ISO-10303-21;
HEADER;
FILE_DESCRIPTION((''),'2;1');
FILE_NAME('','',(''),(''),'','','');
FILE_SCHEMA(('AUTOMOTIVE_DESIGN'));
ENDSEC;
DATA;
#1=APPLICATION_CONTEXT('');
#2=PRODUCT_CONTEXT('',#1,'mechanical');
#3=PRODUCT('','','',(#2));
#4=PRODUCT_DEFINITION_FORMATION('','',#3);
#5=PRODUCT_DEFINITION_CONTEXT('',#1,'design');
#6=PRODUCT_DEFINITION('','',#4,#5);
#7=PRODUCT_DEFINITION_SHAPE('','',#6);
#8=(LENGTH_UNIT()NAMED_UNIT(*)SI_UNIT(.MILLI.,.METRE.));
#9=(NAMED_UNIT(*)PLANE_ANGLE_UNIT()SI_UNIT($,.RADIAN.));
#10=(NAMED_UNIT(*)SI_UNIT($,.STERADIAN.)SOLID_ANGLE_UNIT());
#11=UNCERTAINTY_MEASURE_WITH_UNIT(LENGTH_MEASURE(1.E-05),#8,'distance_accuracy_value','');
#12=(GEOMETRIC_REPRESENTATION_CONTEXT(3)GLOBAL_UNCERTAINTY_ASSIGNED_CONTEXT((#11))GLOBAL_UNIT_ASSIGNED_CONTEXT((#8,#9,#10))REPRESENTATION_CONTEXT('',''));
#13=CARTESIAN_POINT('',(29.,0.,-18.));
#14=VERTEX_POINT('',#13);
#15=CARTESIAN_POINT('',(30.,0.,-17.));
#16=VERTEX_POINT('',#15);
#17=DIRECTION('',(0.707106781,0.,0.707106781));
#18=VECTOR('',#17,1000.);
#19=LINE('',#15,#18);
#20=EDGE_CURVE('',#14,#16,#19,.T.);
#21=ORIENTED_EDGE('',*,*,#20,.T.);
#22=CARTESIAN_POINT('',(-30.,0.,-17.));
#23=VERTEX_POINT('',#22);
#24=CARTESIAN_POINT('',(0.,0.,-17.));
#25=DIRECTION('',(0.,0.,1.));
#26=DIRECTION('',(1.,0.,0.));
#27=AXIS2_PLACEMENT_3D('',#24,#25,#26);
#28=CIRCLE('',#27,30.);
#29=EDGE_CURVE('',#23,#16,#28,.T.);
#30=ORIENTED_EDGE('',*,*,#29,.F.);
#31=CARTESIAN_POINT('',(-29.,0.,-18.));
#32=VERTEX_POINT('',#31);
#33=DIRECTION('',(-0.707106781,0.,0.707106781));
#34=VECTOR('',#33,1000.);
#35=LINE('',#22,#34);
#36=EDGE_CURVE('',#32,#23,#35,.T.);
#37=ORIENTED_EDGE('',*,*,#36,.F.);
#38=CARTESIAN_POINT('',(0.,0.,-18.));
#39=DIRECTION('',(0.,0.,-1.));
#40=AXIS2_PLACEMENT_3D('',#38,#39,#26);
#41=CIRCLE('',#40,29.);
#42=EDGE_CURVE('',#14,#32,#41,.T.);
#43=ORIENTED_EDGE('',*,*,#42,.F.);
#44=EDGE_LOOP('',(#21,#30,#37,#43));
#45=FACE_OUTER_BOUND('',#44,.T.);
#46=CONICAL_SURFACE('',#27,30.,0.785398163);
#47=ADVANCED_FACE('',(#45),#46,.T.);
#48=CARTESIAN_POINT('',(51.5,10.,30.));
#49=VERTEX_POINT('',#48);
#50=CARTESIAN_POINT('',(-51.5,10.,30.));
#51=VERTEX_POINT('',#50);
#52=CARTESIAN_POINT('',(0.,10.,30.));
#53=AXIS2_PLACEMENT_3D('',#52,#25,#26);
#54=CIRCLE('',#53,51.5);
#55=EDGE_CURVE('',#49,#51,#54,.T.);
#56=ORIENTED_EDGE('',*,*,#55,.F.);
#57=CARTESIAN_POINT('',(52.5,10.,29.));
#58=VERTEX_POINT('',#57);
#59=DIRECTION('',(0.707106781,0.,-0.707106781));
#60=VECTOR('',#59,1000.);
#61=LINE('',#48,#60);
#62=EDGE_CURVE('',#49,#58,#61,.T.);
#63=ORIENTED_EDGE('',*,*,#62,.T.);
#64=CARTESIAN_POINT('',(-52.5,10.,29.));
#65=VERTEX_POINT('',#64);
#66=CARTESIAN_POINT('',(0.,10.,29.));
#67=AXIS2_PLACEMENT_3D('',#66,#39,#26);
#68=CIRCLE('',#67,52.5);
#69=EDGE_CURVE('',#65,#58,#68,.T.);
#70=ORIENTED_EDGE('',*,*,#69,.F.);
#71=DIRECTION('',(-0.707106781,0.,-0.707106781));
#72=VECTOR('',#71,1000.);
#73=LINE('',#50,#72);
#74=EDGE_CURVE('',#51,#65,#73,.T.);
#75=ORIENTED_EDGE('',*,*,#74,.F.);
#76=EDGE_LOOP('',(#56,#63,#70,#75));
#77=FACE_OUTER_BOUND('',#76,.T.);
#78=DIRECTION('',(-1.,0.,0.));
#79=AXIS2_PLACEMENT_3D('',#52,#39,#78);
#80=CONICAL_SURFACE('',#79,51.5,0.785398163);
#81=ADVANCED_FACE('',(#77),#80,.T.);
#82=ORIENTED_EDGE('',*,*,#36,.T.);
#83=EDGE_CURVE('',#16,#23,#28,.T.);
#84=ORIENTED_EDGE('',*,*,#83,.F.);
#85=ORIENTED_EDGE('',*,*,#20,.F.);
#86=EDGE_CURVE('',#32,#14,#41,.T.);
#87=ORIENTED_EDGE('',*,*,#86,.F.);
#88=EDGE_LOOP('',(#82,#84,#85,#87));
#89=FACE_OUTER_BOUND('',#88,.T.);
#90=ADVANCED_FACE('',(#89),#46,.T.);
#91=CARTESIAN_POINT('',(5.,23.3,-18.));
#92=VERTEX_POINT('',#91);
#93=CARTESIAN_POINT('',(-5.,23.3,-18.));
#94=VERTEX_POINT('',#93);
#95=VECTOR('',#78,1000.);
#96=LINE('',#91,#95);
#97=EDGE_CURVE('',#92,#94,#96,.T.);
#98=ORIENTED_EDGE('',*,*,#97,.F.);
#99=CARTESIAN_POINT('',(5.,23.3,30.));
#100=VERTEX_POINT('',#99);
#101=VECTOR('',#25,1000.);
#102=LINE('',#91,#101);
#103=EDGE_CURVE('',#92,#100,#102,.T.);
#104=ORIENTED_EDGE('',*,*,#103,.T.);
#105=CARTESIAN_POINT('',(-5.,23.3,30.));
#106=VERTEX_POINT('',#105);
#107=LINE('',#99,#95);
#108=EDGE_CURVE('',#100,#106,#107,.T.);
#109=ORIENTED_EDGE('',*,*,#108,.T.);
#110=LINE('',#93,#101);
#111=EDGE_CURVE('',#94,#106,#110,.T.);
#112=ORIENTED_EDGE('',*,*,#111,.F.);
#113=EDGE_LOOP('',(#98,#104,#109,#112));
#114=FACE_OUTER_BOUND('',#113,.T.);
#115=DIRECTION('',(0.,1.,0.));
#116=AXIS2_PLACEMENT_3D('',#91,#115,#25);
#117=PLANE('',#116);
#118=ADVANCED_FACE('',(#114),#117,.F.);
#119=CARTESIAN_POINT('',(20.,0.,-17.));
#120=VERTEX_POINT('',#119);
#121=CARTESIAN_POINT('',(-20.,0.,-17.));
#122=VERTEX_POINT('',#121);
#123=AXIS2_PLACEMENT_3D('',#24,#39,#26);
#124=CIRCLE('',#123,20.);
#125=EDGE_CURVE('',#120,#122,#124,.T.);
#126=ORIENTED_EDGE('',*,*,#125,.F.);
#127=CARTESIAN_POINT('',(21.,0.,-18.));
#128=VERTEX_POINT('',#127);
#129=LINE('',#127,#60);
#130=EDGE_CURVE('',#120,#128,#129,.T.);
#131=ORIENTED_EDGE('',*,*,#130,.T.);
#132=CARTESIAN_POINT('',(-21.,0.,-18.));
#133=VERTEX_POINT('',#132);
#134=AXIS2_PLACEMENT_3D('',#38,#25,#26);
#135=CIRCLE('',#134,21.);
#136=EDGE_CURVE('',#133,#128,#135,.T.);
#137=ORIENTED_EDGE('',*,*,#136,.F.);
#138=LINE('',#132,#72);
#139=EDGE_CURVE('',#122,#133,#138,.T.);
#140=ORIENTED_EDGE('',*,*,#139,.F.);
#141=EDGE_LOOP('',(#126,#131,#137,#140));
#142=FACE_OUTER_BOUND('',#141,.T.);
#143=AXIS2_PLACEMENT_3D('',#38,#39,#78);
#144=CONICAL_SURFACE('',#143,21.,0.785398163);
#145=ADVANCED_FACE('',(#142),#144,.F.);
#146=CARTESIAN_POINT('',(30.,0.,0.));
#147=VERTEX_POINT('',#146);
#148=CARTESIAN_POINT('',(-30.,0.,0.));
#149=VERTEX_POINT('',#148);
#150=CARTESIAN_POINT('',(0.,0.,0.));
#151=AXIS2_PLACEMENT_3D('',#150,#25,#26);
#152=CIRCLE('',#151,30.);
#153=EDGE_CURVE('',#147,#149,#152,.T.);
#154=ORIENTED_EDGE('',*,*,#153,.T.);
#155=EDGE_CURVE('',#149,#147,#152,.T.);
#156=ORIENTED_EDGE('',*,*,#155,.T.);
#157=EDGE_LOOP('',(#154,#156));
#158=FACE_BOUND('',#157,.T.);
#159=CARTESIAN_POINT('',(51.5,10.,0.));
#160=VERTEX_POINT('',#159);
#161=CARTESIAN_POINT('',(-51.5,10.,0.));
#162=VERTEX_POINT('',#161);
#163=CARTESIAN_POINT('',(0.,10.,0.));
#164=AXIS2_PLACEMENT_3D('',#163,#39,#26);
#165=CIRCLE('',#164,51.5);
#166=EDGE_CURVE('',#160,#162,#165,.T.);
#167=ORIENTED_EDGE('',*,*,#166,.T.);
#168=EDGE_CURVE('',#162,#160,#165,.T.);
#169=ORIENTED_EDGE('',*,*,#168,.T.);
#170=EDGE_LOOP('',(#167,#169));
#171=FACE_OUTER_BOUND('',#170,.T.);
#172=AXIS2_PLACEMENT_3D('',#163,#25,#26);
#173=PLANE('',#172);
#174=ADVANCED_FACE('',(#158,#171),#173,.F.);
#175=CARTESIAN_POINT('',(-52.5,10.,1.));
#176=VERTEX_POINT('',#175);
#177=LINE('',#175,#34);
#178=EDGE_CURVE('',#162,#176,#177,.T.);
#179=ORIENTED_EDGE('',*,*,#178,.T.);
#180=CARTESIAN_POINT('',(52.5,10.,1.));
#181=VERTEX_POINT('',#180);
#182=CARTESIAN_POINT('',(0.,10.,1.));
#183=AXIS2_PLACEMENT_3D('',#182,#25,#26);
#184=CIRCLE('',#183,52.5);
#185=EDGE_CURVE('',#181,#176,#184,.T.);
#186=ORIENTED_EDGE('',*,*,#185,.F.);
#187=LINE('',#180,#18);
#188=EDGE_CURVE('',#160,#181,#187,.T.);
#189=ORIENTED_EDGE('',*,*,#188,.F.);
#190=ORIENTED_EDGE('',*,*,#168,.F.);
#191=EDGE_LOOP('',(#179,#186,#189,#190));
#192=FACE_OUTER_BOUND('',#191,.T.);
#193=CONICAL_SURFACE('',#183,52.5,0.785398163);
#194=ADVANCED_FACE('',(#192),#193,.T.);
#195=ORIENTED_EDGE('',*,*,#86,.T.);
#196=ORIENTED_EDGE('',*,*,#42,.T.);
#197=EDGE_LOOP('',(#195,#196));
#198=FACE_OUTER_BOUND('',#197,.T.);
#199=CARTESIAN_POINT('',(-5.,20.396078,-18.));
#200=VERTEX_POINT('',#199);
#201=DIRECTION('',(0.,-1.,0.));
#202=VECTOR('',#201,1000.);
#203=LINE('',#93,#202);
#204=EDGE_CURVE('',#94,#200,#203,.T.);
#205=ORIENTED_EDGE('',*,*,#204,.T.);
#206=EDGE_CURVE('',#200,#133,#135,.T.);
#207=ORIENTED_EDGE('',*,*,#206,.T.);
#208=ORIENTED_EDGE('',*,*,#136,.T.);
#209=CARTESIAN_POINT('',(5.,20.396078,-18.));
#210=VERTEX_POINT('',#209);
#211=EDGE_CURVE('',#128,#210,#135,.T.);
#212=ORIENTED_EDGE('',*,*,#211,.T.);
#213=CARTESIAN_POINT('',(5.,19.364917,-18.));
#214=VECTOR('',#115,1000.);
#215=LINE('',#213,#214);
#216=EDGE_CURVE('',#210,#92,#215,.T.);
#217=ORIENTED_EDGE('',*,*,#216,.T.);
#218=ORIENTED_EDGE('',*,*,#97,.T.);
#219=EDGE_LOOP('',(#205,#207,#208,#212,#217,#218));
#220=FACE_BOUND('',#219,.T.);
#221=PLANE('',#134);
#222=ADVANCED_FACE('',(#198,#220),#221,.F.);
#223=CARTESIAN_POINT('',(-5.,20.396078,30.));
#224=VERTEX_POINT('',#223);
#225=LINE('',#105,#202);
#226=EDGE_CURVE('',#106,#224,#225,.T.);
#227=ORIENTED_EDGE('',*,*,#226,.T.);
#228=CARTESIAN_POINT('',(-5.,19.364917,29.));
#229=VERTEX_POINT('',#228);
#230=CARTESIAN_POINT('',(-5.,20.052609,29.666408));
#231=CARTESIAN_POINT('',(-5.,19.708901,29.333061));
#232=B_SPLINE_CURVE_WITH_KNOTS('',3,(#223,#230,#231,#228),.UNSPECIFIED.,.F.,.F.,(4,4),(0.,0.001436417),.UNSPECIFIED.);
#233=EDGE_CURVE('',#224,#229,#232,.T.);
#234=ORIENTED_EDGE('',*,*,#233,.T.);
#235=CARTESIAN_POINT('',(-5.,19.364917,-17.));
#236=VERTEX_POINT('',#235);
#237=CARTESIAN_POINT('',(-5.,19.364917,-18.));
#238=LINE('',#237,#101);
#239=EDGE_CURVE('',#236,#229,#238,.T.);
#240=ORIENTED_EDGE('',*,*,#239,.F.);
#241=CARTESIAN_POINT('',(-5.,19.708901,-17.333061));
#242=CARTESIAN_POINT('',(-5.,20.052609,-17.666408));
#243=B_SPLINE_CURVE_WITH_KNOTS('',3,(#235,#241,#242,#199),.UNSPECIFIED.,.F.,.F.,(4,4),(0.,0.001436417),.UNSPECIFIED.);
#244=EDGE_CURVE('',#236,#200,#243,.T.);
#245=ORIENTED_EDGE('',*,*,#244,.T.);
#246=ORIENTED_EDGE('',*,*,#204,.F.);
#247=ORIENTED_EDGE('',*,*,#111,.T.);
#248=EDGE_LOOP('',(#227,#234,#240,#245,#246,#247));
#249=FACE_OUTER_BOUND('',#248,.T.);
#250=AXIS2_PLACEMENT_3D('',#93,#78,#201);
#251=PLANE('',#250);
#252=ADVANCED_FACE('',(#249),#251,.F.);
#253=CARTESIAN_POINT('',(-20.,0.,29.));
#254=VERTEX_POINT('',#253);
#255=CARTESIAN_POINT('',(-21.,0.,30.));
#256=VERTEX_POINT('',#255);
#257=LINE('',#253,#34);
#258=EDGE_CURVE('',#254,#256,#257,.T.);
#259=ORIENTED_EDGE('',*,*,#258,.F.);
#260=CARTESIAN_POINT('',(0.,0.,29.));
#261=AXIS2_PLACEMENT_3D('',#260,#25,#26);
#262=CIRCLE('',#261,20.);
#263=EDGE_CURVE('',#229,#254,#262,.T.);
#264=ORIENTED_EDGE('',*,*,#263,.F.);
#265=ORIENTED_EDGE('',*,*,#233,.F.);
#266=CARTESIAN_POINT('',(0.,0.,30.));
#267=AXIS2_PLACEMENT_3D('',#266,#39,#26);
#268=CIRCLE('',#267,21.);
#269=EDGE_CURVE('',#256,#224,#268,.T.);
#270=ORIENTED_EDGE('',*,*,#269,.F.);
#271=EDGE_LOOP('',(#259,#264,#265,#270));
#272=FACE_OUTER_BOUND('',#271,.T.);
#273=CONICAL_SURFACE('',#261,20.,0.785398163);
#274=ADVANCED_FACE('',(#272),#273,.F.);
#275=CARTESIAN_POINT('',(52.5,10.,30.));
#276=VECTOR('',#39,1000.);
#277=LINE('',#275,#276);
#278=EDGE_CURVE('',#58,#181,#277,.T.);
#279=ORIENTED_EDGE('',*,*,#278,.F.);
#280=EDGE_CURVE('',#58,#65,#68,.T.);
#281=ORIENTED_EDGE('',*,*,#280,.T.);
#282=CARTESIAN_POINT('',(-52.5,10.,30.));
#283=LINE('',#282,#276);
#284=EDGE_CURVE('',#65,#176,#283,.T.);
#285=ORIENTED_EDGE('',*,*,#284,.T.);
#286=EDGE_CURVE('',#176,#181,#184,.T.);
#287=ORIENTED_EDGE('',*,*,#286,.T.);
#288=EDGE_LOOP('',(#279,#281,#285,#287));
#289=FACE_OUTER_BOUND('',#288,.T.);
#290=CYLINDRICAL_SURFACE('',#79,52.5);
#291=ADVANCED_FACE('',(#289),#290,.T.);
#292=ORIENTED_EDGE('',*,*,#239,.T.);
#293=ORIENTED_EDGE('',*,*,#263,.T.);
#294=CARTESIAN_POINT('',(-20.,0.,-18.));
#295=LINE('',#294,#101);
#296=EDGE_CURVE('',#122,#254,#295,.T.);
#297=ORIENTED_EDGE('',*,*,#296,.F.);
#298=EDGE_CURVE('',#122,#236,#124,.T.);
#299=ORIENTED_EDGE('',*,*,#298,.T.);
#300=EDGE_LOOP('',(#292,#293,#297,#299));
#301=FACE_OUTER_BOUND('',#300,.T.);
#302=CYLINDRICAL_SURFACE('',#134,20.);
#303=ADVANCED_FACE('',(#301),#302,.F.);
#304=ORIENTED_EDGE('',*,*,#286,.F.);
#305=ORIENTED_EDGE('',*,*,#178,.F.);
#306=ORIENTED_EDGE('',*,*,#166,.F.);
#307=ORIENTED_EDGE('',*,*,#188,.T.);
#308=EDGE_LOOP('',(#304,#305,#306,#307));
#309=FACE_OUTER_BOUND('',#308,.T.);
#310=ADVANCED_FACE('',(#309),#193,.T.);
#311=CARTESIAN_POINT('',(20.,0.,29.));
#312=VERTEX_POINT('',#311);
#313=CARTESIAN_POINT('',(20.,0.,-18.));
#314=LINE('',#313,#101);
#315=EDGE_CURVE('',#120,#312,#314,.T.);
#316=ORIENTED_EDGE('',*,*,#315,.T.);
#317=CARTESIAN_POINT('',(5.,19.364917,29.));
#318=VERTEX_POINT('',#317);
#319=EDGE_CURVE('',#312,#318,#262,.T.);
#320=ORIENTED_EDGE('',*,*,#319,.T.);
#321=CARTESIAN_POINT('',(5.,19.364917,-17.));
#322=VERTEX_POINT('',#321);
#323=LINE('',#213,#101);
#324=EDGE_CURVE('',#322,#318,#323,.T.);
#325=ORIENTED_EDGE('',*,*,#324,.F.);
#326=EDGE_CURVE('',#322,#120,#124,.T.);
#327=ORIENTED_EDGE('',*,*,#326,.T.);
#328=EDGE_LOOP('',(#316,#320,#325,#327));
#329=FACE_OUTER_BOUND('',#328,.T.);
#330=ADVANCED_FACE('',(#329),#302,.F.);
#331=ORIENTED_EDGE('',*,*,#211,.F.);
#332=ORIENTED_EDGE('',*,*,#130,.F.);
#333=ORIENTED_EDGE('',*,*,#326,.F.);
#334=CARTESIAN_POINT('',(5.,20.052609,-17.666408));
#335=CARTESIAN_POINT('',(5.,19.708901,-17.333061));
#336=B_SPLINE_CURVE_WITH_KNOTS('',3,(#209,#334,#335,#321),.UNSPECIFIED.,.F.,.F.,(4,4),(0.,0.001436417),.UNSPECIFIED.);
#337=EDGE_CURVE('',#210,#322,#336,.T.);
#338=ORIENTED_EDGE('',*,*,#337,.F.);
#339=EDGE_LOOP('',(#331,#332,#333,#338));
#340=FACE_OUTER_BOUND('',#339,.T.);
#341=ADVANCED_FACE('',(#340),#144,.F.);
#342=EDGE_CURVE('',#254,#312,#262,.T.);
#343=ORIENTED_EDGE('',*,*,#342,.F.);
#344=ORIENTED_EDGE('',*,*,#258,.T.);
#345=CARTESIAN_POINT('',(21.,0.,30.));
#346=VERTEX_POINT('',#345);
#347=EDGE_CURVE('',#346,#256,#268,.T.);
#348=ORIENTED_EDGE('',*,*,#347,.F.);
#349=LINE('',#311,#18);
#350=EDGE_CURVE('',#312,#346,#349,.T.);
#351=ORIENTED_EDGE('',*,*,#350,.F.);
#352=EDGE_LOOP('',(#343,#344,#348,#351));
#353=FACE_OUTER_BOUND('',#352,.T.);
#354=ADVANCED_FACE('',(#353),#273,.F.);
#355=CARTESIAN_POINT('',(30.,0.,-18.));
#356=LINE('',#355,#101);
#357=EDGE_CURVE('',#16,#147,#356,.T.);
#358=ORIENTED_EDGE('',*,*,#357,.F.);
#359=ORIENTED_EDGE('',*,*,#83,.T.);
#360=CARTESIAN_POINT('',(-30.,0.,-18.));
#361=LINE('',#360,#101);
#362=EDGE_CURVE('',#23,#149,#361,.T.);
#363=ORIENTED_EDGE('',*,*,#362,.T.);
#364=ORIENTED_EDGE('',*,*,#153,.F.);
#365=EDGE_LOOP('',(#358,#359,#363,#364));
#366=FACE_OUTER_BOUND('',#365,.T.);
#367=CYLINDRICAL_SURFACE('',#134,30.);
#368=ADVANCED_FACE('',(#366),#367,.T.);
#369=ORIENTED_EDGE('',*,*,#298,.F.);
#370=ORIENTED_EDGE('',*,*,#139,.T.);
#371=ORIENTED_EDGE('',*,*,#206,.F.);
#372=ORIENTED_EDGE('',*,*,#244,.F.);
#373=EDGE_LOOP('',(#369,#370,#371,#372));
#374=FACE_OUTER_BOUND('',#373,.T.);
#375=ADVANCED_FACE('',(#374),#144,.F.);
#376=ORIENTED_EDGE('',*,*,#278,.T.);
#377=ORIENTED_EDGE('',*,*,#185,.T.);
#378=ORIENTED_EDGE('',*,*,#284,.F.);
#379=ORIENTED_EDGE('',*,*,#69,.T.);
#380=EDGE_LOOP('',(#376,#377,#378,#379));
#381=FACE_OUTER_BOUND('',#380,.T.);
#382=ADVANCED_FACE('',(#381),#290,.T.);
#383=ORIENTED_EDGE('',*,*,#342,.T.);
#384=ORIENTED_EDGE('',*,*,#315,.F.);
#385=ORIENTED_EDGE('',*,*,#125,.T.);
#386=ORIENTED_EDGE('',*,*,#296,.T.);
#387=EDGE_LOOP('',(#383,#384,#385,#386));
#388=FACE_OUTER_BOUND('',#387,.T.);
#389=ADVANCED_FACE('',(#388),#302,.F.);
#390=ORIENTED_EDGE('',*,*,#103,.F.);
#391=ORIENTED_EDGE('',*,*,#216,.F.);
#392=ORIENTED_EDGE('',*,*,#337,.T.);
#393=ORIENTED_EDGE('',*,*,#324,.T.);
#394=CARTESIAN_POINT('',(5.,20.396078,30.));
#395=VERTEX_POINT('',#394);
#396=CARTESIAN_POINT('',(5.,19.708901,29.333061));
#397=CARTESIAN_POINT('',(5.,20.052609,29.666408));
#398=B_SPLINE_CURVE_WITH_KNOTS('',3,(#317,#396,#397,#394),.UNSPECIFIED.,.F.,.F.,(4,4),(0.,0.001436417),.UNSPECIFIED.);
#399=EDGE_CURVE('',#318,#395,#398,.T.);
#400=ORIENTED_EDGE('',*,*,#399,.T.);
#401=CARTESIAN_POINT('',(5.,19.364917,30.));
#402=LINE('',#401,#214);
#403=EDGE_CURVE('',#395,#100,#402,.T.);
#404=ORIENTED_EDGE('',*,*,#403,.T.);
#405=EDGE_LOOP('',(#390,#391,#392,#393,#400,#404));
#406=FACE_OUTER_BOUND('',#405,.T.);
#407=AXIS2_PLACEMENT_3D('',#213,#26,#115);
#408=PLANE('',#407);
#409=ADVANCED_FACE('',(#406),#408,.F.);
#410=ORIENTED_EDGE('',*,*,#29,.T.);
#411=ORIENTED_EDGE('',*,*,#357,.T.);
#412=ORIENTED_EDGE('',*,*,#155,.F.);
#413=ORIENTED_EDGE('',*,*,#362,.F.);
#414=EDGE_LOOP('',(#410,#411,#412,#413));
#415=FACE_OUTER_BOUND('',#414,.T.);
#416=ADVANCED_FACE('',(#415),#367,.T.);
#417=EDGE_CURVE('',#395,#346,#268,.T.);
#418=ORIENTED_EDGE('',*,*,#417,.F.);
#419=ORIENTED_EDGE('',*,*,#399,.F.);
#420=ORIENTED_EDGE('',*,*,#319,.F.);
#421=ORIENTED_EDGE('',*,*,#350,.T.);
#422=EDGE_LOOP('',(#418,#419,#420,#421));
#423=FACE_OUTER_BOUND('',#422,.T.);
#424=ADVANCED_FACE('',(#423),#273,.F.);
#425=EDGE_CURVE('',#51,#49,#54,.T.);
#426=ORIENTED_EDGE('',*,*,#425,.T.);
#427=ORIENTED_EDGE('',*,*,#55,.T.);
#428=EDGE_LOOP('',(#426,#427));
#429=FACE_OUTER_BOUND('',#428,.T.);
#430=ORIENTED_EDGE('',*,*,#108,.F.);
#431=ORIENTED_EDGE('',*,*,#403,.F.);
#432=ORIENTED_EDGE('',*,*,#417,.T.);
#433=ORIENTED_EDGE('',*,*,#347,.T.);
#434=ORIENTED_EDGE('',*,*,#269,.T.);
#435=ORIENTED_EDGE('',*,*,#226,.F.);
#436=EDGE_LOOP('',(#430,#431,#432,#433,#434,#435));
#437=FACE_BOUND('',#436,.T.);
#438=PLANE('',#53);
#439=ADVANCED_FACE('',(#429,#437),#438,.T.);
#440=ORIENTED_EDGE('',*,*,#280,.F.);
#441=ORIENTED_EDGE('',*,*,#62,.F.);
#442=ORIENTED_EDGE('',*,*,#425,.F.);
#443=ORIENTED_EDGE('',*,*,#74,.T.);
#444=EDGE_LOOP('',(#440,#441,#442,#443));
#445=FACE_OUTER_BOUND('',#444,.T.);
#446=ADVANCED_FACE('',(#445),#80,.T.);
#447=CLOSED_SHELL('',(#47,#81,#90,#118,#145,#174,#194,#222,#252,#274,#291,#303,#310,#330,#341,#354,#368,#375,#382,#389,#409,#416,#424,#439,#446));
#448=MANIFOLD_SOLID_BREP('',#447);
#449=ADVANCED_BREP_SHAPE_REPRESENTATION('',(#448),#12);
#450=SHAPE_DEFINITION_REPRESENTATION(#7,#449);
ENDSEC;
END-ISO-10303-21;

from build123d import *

# Parameters (mm, degrees)
SKETCH_1_4_R       = 52.5
EXTRUDE1_DEPTH     = 30
SKETCH_1_3_R       = 30
EXTRUDE2_DEPTH     = 18
CUT_EXTRUDE1_DEPTH = 87.962635655
CHAMFER1_SIZE      = 1


with BuildPart() as part:
    # Sketch 1_4 → Extrude1 (new body)
    with BuildSketch(Plane.XY):
        with Locations((0, 10)):
            Circle(SKETCH_1_4_R)
    extrude(amount=EXTRUDE1_DEPTH)

    # 草图1<3> → Extrude2 (add)
    with BuildSketch(Plane.XY):
        Circle(SKETCH_1_3_R)
        with BuildLine():
            Line((5, 19.364916731), (5, 23.3))
            Line((5, 23.3), (-5, 23.3))
            Line((-5, 23.3), (-5, 19.364916731))
            ThreePointArc((-5, 19.364916731), (0, -20), (5, 19.364916731))
        make_face(mode=Mode.SUBTRACT)
    extrude(amount=-EXTRUDE2_DEPTH)

    # Sketch 1_4 2 → Cut-Extrude1 (cut, through all)
    with BuildSketch(Plane.XY):
        with BuildLine():
            Line((5, 19.364916731), (5, 23.3))
            Line((5, 23.3), (-5, 23.3))
            Line((-5, 23.3), (-5, 19.364916731))
            ThreePointArc((-5, 19.364916731), (0, -20), (5, 19.364916731))
        make_face()
    extrude(amount=CUT_EXTRUDE1_DEPTH, mode=Mode.SUBTRACT)

    # Chamfer1
    chamfer1_edges = [part.edges().sort_by_distance(p)[0] for p in [
        (-52.5, 10, 0),
        (0, -20, 30),
        (-52.5, 10, 30),
        (-30, 0, -18),
        (0, -20, -18),
    ]]
    chamfer(chamfer1_edges, length=CHAMFER1_SIZE)


solid = part.part
